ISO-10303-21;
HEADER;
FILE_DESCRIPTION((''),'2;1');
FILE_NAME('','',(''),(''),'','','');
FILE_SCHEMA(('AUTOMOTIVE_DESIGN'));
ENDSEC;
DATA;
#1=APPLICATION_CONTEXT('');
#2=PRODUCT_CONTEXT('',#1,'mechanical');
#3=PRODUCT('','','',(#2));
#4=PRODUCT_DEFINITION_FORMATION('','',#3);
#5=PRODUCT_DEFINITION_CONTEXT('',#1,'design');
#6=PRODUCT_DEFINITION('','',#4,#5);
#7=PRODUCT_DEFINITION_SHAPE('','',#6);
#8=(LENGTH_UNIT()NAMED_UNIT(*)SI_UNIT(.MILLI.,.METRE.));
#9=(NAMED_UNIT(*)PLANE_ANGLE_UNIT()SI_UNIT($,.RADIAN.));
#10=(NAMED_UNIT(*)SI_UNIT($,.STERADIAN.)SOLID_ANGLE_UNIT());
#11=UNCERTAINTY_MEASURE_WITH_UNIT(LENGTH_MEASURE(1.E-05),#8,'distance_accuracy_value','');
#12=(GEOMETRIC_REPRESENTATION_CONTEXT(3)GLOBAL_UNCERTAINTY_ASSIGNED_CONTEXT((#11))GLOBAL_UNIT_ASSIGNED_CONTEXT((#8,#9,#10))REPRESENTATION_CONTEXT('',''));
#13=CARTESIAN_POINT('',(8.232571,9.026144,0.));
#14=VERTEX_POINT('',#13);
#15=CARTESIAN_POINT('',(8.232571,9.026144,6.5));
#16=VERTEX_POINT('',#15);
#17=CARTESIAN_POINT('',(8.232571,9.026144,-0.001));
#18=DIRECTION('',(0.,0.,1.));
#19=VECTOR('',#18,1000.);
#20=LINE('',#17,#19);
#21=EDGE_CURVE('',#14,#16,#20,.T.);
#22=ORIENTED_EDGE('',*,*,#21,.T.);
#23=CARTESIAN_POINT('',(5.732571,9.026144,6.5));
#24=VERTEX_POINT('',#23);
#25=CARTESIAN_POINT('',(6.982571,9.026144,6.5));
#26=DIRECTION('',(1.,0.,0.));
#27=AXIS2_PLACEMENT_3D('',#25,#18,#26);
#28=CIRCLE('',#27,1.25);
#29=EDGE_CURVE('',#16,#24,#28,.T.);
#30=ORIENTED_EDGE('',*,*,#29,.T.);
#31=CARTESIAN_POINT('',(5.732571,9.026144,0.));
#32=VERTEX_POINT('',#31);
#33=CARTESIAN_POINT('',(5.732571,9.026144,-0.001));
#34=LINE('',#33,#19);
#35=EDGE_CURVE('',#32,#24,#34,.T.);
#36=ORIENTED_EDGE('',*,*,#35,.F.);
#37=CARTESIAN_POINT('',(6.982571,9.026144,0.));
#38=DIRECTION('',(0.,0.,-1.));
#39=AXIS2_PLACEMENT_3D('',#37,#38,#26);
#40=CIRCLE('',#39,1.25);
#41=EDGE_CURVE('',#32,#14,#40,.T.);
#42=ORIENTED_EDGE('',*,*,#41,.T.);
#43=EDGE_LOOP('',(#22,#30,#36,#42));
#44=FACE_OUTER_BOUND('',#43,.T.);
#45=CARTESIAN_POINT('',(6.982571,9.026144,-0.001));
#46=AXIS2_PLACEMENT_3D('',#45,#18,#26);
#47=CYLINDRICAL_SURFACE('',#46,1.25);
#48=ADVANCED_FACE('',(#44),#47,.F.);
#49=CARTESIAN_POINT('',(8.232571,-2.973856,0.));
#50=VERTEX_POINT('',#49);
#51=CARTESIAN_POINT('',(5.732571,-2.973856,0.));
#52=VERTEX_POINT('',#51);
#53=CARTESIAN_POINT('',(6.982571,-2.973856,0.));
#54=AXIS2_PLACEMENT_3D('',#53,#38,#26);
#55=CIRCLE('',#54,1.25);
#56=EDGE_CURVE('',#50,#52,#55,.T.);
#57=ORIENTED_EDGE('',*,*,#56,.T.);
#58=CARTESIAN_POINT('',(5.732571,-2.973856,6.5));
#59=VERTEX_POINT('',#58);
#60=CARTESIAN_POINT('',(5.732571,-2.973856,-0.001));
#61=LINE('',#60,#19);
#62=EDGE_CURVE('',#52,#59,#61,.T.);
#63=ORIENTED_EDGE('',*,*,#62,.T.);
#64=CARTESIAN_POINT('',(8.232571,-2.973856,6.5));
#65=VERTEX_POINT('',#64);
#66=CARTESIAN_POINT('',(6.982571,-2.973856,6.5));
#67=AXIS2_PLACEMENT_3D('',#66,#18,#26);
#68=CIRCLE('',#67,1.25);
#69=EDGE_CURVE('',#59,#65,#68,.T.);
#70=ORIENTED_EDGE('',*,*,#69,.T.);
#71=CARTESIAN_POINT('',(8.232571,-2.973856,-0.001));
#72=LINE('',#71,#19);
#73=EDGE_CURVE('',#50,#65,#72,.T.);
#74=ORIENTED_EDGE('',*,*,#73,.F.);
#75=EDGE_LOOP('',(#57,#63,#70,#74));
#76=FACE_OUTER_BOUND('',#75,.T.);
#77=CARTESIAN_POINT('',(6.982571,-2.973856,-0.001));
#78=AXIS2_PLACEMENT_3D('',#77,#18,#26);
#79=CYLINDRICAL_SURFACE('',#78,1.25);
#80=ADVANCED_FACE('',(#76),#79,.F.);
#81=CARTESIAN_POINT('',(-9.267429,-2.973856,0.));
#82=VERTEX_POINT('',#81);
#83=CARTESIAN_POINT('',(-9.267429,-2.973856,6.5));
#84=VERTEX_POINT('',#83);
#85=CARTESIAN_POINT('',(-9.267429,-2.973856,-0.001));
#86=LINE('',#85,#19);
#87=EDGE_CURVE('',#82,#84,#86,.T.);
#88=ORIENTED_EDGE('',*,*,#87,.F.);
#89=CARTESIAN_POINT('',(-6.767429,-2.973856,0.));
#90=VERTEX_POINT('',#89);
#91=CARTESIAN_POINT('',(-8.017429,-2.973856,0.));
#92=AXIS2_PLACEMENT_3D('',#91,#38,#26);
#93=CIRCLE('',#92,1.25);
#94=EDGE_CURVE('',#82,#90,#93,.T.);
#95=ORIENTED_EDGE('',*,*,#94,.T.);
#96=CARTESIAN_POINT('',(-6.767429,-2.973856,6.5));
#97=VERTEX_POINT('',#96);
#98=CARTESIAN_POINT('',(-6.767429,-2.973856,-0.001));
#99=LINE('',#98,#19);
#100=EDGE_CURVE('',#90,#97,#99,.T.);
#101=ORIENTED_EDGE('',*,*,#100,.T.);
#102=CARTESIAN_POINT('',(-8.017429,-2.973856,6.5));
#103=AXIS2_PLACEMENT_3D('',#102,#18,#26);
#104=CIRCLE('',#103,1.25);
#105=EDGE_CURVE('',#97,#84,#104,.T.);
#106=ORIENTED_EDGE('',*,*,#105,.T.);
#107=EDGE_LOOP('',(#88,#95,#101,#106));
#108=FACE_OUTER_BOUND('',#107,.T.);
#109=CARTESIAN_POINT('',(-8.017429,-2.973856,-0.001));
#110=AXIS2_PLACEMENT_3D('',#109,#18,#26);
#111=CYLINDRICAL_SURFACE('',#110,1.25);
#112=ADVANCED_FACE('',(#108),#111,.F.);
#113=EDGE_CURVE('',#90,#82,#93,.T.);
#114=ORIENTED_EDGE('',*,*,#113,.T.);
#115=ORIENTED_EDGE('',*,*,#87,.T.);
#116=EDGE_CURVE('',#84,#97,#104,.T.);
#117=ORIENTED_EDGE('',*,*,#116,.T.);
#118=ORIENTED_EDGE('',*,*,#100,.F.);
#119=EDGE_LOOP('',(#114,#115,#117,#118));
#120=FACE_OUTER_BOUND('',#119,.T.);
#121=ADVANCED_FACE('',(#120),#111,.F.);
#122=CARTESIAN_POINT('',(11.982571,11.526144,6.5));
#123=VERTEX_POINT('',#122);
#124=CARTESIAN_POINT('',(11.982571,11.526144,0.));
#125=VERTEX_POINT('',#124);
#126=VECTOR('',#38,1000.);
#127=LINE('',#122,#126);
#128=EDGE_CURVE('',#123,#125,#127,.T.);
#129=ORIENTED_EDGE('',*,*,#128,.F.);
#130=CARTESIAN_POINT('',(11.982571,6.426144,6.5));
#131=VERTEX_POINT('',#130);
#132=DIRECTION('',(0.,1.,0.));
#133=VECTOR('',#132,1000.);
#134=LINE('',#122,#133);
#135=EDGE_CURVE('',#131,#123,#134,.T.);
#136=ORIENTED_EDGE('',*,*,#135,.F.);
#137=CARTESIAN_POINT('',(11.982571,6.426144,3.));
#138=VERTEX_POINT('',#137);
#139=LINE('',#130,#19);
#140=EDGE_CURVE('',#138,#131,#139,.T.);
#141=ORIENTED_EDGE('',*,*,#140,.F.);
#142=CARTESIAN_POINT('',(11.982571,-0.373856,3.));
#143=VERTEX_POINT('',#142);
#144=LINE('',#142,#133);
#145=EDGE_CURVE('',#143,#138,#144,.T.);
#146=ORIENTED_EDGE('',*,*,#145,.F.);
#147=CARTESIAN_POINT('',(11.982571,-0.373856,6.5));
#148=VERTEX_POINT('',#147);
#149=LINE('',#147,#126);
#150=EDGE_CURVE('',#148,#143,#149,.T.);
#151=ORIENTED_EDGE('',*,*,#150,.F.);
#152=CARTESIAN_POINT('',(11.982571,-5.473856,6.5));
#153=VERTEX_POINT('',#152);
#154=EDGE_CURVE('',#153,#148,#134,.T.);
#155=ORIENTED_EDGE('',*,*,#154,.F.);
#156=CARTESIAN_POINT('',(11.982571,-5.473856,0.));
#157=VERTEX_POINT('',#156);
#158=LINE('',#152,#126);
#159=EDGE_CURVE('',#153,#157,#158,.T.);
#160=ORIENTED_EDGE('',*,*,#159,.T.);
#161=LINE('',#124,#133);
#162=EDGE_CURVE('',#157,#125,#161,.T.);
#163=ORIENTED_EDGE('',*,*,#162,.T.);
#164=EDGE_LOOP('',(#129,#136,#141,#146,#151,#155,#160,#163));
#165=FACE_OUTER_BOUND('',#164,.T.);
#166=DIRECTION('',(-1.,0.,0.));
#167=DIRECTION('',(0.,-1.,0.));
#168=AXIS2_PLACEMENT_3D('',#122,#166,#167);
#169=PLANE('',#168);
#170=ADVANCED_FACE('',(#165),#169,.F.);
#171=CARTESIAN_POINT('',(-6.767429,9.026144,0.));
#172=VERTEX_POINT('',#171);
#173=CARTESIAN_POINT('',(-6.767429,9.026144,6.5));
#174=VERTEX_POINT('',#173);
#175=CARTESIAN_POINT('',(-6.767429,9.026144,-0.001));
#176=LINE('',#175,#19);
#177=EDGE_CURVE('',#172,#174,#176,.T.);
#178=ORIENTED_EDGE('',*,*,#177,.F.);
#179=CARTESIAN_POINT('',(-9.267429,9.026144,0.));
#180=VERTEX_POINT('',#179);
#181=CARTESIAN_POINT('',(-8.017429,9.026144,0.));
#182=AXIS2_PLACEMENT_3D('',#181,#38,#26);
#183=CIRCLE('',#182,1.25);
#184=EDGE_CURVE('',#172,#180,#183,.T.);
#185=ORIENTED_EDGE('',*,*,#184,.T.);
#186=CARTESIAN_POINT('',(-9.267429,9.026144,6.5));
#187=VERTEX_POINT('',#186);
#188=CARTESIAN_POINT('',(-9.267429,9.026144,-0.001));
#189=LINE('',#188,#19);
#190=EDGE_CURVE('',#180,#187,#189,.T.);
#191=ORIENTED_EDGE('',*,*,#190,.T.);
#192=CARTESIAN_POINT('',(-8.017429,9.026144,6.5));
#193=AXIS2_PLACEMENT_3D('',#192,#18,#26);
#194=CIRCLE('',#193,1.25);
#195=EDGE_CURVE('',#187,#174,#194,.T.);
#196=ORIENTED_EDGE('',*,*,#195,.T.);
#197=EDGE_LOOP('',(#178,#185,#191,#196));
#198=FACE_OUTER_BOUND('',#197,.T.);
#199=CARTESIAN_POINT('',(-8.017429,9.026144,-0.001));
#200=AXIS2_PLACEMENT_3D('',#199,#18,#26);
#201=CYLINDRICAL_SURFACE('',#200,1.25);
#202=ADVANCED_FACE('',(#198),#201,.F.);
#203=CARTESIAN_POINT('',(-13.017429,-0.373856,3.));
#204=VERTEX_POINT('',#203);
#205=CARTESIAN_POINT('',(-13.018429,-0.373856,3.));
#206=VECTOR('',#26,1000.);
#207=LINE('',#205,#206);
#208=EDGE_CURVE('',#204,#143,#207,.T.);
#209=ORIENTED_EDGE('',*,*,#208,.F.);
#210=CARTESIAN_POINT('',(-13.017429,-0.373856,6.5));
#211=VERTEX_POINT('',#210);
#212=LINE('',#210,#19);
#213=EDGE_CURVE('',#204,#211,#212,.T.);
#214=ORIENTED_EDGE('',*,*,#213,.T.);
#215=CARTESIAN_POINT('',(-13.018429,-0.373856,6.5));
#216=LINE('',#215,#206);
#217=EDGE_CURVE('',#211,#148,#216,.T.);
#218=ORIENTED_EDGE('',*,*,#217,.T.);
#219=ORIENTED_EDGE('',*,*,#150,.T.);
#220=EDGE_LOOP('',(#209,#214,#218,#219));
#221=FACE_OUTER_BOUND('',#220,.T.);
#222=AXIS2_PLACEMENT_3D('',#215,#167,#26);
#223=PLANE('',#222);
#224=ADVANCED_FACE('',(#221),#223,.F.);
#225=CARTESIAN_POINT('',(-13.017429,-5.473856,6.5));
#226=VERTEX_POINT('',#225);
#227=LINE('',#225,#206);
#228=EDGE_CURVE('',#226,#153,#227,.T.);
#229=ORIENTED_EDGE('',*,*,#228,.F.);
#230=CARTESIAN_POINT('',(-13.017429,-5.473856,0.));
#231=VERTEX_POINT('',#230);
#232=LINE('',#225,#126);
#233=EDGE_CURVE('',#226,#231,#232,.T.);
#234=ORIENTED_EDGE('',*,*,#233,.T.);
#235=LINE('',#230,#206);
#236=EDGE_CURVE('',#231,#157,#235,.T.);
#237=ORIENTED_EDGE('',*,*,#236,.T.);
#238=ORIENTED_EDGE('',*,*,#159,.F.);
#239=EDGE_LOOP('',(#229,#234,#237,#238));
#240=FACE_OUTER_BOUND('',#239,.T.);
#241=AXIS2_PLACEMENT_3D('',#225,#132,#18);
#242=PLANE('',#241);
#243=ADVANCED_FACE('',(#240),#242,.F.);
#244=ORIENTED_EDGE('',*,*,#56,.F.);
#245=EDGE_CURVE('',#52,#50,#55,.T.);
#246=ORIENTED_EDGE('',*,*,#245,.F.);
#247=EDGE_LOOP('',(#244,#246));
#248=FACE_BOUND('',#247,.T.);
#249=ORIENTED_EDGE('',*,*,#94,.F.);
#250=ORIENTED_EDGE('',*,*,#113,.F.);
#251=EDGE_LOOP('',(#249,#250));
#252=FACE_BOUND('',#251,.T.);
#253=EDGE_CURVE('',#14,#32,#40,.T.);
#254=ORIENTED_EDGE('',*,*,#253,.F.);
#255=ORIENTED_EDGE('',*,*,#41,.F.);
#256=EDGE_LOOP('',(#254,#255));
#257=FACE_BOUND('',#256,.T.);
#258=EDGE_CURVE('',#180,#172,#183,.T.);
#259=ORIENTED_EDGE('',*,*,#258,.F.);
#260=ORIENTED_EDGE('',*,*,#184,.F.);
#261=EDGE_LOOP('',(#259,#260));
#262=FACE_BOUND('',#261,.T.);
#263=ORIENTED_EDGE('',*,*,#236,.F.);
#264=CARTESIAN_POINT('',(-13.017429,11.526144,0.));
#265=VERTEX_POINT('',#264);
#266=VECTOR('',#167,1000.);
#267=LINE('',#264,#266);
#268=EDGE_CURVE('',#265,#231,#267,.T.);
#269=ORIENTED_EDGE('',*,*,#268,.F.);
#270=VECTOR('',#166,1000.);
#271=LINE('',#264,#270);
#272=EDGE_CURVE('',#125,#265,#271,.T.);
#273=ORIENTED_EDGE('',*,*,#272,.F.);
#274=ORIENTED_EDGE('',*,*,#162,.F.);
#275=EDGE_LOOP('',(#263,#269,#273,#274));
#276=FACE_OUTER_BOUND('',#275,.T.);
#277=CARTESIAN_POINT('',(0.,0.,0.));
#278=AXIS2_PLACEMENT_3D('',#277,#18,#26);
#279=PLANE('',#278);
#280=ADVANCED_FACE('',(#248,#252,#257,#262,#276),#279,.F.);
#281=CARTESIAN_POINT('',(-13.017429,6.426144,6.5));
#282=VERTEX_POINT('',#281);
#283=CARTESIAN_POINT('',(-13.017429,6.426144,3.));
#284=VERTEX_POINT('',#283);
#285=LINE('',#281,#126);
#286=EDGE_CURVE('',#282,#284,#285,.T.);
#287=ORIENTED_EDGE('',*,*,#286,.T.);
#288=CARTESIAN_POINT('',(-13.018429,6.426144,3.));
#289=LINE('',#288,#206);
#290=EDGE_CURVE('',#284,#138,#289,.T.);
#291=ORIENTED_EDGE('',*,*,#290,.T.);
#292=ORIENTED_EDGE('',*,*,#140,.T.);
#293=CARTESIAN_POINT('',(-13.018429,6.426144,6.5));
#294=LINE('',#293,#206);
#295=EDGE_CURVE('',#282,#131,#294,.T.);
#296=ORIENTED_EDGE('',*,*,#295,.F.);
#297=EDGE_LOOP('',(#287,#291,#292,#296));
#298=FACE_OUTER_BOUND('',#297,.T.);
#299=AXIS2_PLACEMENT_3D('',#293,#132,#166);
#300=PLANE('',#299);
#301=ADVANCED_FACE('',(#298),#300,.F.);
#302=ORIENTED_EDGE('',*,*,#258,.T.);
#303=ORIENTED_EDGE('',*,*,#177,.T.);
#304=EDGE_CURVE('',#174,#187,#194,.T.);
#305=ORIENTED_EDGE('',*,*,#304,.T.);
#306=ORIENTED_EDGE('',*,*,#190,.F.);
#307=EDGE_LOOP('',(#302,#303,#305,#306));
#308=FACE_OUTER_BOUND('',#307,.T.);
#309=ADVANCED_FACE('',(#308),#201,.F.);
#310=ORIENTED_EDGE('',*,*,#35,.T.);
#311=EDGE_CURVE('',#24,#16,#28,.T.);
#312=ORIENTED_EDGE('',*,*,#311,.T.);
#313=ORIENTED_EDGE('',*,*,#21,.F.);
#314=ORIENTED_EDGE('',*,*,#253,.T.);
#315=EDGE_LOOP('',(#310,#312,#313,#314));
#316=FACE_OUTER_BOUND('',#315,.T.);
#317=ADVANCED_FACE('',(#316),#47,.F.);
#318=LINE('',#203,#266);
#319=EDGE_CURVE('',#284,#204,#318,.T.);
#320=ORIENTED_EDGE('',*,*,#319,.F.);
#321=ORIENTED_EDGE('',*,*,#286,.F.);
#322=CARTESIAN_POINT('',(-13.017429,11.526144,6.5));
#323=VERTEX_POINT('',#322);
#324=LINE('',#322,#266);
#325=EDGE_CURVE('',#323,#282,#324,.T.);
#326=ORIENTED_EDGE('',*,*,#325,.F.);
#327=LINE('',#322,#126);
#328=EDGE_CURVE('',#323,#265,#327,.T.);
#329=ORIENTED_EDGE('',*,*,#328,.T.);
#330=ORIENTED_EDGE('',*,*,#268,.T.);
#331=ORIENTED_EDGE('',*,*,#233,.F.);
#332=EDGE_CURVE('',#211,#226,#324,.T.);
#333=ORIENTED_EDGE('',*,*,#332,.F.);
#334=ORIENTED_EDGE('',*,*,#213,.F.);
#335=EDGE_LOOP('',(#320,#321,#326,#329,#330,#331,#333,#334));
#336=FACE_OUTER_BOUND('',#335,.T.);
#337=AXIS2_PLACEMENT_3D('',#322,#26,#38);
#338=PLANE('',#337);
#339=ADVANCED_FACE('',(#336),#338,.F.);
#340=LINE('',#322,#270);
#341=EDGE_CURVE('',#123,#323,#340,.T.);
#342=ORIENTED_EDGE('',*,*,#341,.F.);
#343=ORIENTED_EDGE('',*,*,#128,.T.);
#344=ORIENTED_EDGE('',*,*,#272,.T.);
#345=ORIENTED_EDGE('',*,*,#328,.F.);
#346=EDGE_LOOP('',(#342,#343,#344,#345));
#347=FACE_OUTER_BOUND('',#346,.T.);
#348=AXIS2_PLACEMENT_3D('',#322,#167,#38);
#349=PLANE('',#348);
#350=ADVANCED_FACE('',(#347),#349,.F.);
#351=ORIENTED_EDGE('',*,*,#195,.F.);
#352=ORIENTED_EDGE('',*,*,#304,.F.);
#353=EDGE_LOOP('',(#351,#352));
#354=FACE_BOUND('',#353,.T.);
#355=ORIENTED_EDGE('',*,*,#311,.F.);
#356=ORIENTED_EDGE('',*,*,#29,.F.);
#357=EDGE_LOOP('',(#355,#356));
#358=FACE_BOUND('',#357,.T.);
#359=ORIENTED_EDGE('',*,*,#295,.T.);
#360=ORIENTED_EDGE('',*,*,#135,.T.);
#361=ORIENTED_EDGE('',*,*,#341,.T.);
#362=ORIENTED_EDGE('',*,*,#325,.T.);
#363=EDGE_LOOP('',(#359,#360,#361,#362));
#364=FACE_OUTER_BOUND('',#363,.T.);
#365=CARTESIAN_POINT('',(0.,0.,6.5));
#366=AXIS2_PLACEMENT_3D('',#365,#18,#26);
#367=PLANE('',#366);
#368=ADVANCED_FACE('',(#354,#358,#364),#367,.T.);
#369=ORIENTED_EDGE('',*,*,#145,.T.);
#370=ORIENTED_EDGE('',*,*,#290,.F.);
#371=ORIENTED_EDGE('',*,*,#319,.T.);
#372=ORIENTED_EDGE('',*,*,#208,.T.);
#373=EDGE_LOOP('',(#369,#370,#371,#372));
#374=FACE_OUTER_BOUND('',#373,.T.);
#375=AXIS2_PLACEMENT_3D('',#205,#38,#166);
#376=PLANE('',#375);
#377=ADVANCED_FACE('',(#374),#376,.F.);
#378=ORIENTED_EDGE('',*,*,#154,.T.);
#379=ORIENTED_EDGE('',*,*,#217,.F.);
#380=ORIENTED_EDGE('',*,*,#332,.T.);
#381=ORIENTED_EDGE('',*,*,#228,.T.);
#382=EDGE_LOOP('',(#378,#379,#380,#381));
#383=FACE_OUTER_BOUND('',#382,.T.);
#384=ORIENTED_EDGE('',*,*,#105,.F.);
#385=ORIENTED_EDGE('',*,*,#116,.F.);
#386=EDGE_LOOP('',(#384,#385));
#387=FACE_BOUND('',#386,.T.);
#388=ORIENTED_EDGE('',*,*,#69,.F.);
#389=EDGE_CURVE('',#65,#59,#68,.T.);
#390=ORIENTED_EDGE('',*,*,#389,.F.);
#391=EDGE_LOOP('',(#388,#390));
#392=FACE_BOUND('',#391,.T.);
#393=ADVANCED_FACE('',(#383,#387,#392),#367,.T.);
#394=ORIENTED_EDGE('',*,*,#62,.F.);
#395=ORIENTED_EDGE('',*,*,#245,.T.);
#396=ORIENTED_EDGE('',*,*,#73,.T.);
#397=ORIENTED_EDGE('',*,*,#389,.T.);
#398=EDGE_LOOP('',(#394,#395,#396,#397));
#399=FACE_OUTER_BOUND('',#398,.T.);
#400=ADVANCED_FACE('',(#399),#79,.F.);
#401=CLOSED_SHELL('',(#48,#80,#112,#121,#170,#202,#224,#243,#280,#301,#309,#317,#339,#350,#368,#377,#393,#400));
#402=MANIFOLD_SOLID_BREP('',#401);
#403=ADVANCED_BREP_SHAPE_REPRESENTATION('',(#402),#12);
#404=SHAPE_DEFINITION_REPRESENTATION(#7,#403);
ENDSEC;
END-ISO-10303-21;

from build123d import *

# Parameters (mm, degrees)
SKETCH_1_W          = 25
SKETCH_1_H          = 17
EXTRUDE_1_DEPTH     = 6.5
CUT_EXTRUDE_1_REACH = 30.286
SKETCH_2_W          = 3.5
SKETCH_2_H          = 6.8
CUT_EXTRUDE_2_REACH = 20.562
SKETCH_3_R          = 1.25


with BuildPart() as part:
    # 草图1 → 凸台-拉伸1 (new body)
    with BuildSketch(Plane.XY):
        with Locations((-0.517429194, 3.026143791)):
            Rectangle(SKETCH_1_W, SKETCH_1_H)
    extrude(amount=EXTRUDE_1_DEPTH)

    # 草图2 → 切除-拉伸1 (cut, up to next)
    with BuildSketch(Plane(origin=(11.982570806, 0, 0), x_dir=(0, 0, -1), z_dir=(1, 0, 0)), mode=Mode.PRIVATE) as cut_extrude_1_sk1:
        with Locations((-4.75, 3.026143791)):
            Rectangle(SKETCH_2_W, SKETCH_2_H)
    cut_extrude_1_tool1 = extrude(cut_extrude_1_sk1.sketch, amount=-CUT_EXTRUDE_1_REACH, mode=Mode.PRIVATE) & part.part
    add(cut_extrude_1_tool1.solids().sort_by_distance((11.982571, 3.026144, 4.75))[0], mode=Mode.SUBTRACT)

    # 草图3 → 切除-拉伸2 (cut, up to next)
    with BuildSketch(Plane.XY.offset(6.5), mode=Mode.PRIVATE) as cut_extrude_2_sk1:
        with Locations((-8.017429194, 9.026143791)):
            Circle(SKETCH_3_R)
    cut_extrude_2_tool1 = extrude(cut_extrude_2_sk1.sketch, amount=-CUT_EXTRUDE_2_REACH, mode=Mode.PRIVATE) & part.part
    # 草图3 → 切除-拉伸2 (cut, up to next)
    with BuildSketch(Plane.XY.offset(6.5), mode=Mode.PRIVATE) as cut_extrude_2_sk2:
        with Locations((6.982570806, 9.026143791)):
            Circle(SKETCH_3_R)
    cut_extrude_2_tool2 = extrude(cut_extrude_2_sk2.sketch, amount=-CUT_EXTRUDE_2_REACH, mode=Mode.PRIVATE) & part.part
    # 草图3 → 切除-拉伸2 (cut, up to next)
    with BuildSketch(Plane.XY.offset(6.5), mode=Mode.PRIVATE) as cut_extrude_2_sk3:
        with Locations((-8.017429194, -2.973856209)):
            Circle(SKETCH_3_R)
    cut_extrude_2_tool3 = extrude(cut_extrude_2_sk3.sketch, amount=-CUT_EXTRUDE_2_REACH, mode=Mode.PRIVATE) & part.part
    # 草图3 → 切除-拉伸2 (cut, up to next)
    with BuildSketch(Plane.XY.offset(6.5), mode=Mode.PRIVATE) as cut_extrude_2_sk4:
        with Locations((6.982570806, -2.973856209)):
            Circle(SKETCH_3_R)
    cut_extrude_2_tool4 = extrude(cut_extrude_2_sk4.sketch, amount=-CUT_EXTRUDE_2_REACH, mode=Mode.PRIVATE) & part.part
    add(cut_extrude_2_tool1.solids().sort_by_distance((-8.017429, 9.026144, 6.5))[0], mode=Mode.SUBTRACT)
    add(cut_extrude_2_tool2.solids().sort_by_distance((6.982571, 9.026144, 6.5))[0], mode=Mode.SUBTRACT)
    add(cut_extrude_2_tool3.solids().sort_by_distance((-8.017429, -2.973856, 6.5))[0], mode=Mode.SUBTRACT)
    add(cut_extrude_2_tool4.solids().sort_by_distance((6.982571, -2.973856, 6.5))[0], mode=Mode.SUBTRACT)


solid = part.part
